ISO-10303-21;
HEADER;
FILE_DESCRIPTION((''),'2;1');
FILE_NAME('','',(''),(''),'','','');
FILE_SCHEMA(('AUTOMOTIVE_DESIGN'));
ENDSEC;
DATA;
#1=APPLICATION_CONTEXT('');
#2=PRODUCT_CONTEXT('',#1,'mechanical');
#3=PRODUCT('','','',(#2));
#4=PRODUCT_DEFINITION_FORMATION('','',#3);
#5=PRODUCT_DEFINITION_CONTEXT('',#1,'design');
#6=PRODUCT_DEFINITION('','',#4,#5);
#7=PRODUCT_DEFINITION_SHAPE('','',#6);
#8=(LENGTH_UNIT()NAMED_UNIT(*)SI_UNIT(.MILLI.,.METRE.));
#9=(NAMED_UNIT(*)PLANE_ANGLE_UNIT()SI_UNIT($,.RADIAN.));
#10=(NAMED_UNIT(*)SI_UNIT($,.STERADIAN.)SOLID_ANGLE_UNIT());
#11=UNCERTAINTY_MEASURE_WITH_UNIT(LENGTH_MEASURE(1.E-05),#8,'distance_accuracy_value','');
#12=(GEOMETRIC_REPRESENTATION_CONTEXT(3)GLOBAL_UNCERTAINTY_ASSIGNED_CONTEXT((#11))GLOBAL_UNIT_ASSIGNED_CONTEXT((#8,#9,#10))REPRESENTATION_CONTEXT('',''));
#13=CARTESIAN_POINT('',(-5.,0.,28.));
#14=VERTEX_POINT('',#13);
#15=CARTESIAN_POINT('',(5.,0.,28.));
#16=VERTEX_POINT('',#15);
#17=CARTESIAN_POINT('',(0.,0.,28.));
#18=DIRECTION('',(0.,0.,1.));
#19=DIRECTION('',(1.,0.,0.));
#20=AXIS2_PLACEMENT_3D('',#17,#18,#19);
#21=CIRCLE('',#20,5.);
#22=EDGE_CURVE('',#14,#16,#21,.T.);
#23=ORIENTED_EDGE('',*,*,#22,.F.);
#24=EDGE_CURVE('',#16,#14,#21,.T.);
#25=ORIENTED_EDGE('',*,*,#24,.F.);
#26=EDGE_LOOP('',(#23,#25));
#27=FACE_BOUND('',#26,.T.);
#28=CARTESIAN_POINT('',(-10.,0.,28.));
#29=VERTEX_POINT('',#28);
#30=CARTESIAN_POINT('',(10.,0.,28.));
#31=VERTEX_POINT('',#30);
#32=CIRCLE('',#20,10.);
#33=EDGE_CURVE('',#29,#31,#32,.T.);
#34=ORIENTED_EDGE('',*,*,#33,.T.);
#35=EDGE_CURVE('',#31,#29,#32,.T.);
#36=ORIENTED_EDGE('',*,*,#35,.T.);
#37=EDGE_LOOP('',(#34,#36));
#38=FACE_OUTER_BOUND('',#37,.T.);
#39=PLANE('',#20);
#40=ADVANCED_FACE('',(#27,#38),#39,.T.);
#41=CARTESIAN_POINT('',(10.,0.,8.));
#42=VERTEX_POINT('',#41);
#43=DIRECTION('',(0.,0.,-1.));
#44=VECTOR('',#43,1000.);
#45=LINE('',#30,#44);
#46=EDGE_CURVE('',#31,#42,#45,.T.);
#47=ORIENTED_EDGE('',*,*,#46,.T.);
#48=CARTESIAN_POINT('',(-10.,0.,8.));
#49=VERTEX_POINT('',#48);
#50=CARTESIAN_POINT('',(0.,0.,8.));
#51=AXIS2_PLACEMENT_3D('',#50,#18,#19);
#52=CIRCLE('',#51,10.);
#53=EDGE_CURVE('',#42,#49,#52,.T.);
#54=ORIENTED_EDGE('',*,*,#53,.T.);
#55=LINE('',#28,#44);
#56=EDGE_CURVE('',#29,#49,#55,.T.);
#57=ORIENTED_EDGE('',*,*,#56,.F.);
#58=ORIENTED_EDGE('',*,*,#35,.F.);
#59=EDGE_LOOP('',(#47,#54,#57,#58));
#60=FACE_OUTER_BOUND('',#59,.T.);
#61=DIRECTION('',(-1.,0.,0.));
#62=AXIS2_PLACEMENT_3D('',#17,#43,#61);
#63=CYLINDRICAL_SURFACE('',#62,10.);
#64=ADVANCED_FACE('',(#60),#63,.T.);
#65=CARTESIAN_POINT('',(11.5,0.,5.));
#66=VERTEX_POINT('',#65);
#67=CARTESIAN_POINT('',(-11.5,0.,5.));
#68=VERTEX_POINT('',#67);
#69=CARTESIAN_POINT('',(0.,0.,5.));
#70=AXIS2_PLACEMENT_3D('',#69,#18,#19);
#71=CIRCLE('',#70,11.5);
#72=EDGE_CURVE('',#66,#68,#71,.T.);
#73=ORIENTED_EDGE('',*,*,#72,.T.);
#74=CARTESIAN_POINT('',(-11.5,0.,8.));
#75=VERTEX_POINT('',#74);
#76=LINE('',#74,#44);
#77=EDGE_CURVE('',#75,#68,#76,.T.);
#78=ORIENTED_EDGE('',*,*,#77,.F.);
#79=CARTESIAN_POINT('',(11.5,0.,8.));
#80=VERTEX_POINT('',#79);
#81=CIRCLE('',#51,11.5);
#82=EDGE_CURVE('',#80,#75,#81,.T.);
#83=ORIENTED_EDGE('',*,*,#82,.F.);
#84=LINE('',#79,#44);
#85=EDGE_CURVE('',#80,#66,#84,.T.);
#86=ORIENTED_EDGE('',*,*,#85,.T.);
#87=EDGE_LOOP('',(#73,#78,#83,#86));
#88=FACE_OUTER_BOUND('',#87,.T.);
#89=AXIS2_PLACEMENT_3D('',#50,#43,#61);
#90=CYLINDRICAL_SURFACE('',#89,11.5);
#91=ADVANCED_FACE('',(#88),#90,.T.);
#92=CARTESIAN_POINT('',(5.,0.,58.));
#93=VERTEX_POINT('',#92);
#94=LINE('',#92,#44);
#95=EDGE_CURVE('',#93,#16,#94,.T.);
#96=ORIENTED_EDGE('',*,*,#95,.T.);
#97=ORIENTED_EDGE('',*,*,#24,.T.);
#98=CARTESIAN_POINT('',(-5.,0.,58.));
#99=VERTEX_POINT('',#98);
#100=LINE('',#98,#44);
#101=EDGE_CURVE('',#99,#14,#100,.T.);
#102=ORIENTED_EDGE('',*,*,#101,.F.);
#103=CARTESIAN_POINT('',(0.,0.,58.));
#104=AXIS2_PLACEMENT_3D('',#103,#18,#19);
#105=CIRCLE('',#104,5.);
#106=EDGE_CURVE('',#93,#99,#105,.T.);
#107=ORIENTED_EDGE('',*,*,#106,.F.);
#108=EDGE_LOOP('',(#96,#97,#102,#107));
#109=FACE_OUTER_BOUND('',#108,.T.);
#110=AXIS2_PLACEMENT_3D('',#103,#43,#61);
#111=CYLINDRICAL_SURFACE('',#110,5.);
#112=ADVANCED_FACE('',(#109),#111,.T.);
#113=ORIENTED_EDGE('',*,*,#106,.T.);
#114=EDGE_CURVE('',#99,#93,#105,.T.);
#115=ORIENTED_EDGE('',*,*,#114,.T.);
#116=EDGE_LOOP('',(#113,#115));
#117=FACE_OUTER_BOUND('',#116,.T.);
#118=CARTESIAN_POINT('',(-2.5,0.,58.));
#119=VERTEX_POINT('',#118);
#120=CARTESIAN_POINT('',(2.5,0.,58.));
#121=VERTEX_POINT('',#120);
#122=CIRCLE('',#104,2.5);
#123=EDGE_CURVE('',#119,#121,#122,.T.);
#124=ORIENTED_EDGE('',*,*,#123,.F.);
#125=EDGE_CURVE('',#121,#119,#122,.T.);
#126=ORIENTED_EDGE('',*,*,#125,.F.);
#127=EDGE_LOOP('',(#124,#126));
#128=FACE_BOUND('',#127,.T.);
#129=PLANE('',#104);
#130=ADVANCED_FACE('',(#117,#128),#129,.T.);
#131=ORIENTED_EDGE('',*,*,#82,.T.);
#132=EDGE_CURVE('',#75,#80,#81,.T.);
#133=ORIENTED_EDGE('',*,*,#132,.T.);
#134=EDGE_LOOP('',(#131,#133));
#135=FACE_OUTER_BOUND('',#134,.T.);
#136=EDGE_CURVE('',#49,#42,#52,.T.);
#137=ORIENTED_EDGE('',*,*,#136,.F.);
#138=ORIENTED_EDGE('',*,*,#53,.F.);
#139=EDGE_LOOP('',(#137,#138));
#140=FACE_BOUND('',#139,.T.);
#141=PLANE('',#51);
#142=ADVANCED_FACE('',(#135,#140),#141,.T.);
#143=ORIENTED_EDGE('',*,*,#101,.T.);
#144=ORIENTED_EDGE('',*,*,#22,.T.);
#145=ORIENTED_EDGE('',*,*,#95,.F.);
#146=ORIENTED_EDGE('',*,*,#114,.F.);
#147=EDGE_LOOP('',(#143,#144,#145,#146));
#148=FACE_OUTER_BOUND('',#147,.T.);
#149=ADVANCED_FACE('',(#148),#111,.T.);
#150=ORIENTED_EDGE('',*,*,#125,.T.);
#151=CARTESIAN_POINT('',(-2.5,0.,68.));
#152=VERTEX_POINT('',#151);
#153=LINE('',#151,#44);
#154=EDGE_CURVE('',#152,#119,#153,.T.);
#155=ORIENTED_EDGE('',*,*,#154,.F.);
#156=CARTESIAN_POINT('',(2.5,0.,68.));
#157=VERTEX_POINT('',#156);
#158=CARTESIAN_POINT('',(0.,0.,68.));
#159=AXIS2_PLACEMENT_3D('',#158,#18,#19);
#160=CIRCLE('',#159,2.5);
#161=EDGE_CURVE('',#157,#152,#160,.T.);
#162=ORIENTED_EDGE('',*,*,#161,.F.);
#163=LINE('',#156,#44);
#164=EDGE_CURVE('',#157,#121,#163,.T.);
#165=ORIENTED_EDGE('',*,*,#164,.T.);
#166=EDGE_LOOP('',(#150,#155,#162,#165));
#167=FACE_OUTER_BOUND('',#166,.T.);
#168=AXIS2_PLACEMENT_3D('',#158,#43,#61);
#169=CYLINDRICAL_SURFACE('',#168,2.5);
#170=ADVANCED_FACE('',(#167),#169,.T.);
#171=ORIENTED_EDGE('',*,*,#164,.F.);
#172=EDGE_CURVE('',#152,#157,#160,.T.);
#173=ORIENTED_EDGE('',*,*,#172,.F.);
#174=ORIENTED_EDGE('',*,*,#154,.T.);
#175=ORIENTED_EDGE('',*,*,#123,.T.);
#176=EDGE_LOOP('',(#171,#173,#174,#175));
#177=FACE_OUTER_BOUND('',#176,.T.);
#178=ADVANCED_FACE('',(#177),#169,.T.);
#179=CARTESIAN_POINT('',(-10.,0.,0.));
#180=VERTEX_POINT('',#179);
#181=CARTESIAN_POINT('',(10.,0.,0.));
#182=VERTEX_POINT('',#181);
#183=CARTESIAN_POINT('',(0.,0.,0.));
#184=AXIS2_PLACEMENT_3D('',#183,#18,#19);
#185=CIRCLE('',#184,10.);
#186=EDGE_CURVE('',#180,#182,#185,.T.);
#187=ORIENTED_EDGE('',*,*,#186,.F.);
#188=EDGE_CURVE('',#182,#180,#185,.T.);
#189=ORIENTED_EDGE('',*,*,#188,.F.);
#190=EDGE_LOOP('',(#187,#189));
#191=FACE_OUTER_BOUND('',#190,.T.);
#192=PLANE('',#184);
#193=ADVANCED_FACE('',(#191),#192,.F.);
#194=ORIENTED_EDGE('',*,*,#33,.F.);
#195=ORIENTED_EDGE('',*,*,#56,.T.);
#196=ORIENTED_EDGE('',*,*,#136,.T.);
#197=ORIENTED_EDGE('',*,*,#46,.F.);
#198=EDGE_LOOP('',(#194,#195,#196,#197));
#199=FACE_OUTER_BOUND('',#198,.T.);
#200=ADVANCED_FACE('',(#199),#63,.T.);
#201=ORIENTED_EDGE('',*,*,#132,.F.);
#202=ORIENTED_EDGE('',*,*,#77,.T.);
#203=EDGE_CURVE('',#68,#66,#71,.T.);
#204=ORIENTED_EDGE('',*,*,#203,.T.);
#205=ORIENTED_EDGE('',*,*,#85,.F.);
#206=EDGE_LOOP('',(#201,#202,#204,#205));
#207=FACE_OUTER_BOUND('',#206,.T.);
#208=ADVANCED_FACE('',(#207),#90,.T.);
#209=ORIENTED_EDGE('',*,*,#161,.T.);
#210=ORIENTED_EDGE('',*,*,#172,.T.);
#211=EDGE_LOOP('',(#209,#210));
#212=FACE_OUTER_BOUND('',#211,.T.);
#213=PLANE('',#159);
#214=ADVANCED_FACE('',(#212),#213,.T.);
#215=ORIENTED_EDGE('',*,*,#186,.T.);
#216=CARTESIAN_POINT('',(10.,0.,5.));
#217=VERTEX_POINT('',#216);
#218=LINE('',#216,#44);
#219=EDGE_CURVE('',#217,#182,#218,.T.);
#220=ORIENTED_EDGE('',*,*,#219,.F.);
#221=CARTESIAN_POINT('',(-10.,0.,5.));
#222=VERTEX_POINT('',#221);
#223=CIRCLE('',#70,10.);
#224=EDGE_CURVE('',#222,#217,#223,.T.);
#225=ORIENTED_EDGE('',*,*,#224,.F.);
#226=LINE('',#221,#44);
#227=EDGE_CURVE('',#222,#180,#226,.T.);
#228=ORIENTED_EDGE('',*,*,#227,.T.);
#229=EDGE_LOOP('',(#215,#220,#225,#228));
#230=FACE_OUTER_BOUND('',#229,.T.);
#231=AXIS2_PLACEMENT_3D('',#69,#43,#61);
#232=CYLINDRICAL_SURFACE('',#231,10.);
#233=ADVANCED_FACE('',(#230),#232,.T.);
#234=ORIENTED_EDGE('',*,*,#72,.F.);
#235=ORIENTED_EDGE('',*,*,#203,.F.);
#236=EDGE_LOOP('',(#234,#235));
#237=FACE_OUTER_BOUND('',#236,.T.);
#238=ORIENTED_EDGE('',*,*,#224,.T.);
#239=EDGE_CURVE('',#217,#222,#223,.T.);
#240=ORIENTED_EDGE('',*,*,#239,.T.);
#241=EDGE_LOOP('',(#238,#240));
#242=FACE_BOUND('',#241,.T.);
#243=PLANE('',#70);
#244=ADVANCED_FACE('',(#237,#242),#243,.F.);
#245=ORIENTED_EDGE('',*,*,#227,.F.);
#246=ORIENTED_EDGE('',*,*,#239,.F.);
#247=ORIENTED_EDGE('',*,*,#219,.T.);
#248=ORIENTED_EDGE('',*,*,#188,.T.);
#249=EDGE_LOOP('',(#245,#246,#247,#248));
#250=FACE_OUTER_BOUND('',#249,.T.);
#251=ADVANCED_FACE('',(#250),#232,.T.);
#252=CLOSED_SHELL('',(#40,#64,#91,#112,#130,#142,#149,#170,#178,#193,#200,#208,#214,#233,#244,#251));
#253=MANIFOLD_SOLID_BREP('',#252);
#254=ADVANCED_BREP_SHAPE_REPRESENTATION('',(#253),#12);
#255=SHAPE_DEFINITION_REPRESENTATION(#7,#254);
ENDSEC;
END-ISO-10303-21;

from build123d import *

# Parameters (mm, degrees)
SKETCH1_R           = 10
BOSS_EXTRUDE1_DEPTH = 5
SKETCH2_R           = 11.5
BOSS_EXTRUDE2_DEPTH = 3
SKETCH3_R           = 10
BOSS_EXTRUDE3_DEPTH = 20
SKETCH4_R           = 5
BOSS_EXTRUDE4_DEPTH = 30
SKETCH5_R           = 2.5
BOSS_EXTRUDE5_DEPTH = 10


with BuildPart() as part:
    # Sketch1 → Boss-Extrude1 (new body)
    with BuildSketch(Plane.XY):
        Circle(SKETCH1_R)
    extrude(amount=BOSS_EXTRUDE1_DEPTH)

    # Sketch2 → Boss-Extrude2 (add)
    with BuildSketch(Plane.XY.offset(5)):
        Circle(SKETCH2_R)
    extrude(amount=BOSS_EXTRUDE2_DEPTH)

    # Sketch3 → Boss-Extrude3 (add)
    with BuildSketch(Plane.XY.offset(8)):
        Circle(SKETCH3_R)
    extrude(amount=BOSS_EXTRUDE3_DEPTH)

    # Sketch4 → Boss-Extrude4 (add)
    with BuildSketch(Plane.XY.offset(28)):
        Circle(SKETCH4_R)
    extrude(amount=BOSS_EXTRUDE4_DEPTH)

    # Sketch5 → Boss-Extrude5 (add)
    with BuildSketch(Plane.XY.offset(58)):
        Circle(SKETCH5_R)
    extrude(amount=BOSS_EXTRUDE5_DEPTH)


solid = part.part
